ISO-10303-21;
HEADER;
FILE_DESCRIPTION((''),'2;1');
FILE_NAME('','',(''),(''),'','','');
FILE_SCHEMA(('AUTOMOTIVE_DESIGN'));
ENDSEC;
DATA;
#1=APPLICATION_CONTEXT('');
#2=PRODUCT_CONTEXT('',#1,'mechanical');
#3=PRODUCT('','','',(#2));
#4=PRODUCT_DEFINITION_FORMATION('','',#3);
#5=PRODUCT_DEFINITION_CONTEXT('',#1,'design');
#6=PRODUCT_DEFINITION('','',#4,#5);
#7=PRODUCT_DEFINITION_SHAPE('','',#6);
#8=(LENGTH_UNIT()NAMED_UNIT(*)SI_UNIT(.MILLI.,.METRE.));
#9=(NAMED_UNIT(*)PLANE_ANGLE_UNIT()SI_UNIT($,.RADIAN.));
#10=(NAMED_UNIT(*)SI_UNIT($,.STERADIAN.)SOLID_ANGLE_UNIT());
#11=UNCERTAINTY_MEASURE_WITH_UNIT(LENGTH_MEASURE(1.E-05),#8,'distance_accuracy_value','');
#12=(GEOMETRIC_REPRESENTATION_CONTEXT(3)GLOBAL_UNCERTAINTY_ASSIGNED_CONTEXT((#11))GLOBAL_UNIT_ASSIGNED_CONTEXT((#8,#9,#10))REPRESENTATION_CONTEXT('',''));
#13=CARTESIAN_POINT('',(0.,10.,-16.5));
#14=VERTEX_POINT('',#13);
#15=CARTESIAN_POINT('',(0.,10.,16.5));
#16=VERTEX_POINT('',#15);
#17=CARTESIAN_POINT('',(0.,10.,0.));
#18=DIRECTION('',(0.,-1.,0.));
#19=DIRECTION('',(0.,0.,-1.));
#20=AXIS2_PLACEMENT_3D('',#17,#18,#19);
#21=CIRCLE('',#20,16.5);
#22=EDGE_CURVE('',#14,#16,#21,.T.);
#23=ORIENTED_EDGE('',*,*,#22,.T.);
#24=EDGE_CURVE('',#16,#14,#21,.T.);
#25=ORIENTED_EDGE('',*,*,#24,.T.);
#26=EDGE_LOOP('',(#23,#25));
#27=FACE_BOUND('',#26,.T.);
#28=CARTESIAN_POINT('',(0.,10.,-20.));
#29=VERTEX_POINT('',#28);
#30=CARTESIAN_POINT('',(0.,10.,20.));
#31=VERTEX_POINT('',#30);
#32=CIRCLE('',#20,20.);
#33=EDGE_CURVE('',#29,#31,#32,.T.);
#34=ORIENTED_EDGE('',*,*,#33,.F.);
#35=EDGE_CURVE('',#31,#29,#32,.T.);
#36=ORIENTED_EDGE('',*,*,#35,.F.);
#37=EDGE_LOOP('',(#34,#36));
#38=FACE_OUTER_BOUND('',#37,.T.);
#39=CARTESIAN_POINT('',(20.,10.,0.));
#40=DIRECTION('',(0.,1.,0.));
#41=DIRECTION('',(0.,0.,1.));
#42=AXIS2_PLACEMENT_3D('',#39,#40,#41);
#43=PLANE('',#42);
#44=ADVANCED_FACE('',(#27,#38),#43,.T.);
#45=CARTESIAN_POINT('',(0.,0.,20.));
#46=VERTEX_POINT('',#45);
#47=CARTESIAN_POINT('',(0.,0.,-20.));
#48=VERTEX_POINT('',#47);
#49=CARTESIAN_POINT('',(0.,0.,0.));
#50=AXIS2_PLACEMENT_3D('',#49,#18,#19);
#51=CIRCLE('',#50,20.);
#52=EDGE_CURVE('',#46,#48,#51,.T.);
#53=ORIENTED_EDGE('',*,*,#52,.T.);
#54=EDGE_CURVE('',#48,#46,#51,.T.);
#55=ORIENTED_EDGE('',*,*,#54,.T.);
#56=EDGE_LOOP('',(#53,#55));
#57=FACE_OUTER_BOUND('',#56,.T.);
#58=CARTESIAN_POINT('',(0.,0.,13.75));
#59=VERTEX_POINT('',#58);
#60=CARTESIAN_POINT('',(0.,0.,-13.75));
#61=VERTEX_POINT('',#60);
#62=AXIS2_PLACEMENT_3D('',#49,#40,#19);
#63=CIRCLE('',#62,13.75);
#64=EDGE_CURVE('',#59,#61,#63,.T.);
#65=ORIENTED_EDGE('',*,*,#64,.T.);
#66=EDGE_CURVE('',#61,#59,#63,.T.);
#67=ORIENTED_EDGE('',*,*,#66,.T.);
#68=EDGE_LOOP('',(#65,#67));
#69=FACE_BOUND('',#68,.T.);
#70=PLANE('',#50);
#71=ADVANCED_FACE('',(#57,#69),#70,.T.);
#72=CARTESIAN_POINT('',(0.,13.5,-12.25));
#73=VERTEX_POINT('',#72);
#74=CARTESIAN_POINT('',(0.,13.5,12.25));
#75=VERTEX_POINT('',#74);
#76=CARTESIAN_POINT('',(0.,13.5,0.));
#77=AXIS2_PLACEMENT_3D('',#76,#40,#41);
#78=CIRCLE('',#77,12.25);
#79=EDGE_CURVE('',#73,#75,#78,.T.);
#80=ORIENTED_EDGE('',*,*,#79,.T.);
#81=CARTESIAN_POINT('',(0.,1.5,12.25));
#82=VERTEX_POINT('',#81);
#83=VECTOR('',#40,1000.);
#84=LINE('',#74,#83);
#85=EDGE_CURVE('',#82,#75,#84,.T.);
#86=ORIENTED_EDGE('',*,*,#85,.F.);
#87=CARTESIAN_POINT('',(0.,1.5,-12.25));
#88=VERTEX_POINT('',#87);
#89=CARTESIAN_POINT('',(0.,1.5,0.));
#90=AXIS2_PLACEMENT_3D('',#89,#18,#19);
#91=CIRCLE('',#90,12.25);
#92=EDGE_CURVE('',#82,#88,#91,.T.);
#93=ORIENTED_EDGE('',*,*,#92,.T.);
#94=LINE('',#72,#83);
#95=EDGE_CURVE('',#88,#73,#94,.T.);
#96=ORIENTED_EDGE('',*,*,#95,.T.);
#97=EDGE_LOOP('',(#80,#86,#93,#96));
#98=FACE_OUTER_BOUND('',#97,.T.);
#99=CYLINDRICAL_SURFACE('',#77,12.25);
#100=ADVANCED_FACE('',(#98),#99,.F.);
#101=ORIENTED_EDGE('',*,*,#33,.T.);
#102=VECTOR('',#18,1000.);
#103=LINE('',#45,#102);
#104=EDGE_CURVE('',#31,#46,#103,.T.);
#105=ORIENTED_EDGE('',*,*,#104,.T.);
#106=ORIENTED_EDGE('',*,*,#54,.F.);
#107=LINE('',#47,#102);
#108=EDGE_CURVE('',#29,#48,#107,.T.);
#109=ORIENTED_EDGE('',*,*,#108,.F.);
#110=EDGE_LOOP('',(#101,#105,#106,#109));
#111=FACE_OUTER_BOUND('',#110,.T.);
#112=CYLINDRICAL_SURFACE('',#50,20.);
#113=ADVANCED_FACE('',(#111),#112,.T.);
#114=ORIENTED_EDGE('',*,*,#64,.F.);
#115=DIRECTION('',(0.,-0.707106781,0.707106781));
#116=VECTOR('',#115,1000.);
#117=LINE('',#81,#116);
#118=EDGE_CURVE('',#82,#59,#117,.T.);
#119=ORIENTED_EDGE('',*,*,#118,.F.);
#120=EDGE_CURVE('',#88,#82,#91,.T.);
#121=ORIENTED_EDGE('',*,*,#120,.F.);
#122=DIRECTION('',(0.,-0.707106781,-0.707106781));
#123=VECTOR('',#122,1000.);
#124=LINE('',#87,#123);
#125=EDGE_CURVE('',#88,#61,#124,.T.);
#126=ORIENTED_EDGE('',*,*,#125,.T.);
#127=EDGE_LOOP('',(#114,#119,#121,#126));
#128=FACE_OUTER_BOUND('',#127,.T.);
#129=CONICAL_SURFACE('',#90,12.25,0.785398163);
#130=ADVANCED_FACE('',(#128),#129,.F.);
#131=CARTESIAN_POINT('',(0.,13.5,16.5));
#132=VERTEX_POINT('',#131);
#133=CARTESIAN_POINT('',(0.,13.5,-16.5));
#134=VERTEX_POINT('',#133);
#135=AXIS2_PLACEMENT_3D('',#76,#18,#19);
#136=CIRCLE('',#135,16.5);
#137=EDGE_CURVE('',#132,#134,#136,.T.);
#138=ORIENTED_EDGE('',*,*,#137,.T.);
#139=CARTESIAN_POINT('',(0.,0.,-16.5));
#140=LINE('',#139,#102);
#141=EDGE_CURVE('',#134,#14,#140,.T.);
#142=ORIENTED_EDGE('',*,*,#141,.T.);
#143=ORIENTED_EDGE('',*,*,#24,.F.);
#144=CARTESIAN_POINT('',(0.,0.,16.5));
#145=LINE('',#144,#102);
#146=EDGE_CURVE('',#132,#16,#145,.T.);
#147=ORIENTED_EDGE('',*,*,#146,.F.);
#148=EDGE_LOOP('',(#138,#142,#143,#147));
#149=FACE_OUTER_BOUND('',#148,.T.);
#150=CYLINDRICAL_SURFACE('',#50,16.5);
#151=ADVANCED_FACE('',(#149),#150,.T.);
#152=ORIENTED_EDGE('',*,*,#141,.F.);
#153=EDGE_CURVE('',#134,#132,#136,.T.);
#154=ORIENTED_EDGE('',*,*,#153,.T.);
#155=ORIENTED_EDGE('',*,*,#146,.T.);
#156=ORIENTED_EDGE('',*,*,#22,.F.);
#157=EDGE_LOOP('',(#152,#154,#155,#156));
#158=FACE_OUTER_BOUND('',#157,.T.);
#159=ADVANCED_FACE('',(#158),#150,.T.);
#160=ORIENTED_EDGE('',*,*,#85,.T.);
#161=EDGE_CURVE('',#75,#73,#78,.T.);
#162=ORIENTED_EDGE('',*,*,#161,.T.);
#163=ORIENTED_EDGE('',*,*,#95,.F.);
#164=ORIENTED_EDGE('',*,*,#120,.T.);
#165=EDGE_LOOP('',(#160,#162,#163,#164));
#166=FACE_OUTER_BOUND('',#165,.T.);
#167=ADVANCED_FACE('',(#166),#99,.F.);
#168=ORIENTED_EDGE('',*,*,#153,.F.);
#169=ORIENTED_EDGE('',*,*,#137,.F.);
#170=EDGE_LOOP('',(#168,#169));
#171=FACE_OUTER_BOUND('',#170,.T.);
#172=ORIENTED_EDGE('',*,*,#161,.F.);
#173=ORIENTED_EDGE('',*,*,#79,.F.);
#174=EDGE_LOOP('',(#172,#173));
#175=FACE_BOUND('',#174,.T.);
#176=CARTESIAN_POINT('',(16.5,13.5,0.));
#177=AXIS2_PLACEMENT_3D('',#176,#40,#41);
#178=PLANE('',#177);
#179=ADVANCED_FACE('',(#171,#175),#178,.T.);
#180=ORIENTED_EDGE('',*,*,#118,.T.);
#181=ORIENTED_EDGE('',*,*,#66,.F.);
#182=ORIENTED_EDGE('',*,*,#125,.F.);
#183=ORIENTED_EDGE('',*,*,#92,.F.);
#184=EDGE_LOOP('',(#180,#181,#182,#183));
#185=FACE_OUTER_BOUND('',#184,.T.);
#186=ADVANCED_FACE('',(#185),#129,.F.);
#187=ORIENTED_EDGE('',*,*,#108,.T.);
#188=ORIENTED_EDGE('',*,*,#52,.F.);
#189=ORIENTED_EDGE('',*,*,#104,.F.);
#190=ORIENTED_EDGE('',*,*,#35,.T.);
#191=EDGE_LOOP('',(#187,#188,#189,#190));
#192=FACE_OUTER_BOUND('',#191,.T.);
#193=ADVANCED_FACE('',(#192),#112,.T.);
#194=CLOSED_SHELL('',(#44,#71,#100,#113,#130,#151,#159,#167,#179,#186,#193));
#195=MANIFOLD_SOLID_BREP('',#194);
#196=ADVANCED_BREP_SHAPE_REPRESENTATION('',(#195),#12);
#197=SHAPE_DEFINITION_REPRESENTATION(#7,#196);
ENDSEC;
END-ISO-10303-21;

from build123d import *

# Parameters (mm, degrees)
G3_4_TAPPED_HOLE1_D     = 24.5
G3_4_TAPPED_HOLE1_DEPTH = 58.32
G3_4_TAPPED_HOLE1_TIP   = 7.360542583
CHAMFER1_SIZE           = 1.5


with BuildPart() as part:
    # Sketch1 → Revolve1 (revolve)
    with BuildSketch(Plane.XY, mode=Mode.PRIVATE) as revolve1_sk:
        Polygon((0, 0), (20, 0), (20, 10), (16.5, 10), (16.5, 13.5), (0, 13.5), align=None)
    revolve(revolve1_sk.sketch.rotate(Axis((0, 0, 0), (0, 1, 0)), 90), axis=Axis((0, 0, 0), (0, 1, 0)))

    # G3/4 Tapped Hole1
    with Locations(Plane(origin=(0, 13.5, 0), x_dir=(1, 0, 0), z_dir=(0, 1, 0))):
        with Locations((0, 0)):
            Hole(G3_4_TAPPED_HOLE1_D / 2, depth=G3_4_TAPPED_HOLE1_DEPTH)
            with Locations((0, 0, -(G3_4_TAPPED_HOLE1_DEPTH + G3_4_TAPPED_HOLE1_TIP / 2))):  # 118° drill point
                Cone(0, G3_4_TAPPED_HOLE1_D / 2, G3_4_TAPPED_HOLE1_TIP, mode=Mode.SUBTRACT)

    # Chamfer1
    chamfer1_edges = [part.edges().sort_by_distance(p)[0] for p in [
        (12.25, 0, 0),
    ]]
    chamfer(chamfer1_edges, length=CHAMFER1_SIZE)


solid = part.part
